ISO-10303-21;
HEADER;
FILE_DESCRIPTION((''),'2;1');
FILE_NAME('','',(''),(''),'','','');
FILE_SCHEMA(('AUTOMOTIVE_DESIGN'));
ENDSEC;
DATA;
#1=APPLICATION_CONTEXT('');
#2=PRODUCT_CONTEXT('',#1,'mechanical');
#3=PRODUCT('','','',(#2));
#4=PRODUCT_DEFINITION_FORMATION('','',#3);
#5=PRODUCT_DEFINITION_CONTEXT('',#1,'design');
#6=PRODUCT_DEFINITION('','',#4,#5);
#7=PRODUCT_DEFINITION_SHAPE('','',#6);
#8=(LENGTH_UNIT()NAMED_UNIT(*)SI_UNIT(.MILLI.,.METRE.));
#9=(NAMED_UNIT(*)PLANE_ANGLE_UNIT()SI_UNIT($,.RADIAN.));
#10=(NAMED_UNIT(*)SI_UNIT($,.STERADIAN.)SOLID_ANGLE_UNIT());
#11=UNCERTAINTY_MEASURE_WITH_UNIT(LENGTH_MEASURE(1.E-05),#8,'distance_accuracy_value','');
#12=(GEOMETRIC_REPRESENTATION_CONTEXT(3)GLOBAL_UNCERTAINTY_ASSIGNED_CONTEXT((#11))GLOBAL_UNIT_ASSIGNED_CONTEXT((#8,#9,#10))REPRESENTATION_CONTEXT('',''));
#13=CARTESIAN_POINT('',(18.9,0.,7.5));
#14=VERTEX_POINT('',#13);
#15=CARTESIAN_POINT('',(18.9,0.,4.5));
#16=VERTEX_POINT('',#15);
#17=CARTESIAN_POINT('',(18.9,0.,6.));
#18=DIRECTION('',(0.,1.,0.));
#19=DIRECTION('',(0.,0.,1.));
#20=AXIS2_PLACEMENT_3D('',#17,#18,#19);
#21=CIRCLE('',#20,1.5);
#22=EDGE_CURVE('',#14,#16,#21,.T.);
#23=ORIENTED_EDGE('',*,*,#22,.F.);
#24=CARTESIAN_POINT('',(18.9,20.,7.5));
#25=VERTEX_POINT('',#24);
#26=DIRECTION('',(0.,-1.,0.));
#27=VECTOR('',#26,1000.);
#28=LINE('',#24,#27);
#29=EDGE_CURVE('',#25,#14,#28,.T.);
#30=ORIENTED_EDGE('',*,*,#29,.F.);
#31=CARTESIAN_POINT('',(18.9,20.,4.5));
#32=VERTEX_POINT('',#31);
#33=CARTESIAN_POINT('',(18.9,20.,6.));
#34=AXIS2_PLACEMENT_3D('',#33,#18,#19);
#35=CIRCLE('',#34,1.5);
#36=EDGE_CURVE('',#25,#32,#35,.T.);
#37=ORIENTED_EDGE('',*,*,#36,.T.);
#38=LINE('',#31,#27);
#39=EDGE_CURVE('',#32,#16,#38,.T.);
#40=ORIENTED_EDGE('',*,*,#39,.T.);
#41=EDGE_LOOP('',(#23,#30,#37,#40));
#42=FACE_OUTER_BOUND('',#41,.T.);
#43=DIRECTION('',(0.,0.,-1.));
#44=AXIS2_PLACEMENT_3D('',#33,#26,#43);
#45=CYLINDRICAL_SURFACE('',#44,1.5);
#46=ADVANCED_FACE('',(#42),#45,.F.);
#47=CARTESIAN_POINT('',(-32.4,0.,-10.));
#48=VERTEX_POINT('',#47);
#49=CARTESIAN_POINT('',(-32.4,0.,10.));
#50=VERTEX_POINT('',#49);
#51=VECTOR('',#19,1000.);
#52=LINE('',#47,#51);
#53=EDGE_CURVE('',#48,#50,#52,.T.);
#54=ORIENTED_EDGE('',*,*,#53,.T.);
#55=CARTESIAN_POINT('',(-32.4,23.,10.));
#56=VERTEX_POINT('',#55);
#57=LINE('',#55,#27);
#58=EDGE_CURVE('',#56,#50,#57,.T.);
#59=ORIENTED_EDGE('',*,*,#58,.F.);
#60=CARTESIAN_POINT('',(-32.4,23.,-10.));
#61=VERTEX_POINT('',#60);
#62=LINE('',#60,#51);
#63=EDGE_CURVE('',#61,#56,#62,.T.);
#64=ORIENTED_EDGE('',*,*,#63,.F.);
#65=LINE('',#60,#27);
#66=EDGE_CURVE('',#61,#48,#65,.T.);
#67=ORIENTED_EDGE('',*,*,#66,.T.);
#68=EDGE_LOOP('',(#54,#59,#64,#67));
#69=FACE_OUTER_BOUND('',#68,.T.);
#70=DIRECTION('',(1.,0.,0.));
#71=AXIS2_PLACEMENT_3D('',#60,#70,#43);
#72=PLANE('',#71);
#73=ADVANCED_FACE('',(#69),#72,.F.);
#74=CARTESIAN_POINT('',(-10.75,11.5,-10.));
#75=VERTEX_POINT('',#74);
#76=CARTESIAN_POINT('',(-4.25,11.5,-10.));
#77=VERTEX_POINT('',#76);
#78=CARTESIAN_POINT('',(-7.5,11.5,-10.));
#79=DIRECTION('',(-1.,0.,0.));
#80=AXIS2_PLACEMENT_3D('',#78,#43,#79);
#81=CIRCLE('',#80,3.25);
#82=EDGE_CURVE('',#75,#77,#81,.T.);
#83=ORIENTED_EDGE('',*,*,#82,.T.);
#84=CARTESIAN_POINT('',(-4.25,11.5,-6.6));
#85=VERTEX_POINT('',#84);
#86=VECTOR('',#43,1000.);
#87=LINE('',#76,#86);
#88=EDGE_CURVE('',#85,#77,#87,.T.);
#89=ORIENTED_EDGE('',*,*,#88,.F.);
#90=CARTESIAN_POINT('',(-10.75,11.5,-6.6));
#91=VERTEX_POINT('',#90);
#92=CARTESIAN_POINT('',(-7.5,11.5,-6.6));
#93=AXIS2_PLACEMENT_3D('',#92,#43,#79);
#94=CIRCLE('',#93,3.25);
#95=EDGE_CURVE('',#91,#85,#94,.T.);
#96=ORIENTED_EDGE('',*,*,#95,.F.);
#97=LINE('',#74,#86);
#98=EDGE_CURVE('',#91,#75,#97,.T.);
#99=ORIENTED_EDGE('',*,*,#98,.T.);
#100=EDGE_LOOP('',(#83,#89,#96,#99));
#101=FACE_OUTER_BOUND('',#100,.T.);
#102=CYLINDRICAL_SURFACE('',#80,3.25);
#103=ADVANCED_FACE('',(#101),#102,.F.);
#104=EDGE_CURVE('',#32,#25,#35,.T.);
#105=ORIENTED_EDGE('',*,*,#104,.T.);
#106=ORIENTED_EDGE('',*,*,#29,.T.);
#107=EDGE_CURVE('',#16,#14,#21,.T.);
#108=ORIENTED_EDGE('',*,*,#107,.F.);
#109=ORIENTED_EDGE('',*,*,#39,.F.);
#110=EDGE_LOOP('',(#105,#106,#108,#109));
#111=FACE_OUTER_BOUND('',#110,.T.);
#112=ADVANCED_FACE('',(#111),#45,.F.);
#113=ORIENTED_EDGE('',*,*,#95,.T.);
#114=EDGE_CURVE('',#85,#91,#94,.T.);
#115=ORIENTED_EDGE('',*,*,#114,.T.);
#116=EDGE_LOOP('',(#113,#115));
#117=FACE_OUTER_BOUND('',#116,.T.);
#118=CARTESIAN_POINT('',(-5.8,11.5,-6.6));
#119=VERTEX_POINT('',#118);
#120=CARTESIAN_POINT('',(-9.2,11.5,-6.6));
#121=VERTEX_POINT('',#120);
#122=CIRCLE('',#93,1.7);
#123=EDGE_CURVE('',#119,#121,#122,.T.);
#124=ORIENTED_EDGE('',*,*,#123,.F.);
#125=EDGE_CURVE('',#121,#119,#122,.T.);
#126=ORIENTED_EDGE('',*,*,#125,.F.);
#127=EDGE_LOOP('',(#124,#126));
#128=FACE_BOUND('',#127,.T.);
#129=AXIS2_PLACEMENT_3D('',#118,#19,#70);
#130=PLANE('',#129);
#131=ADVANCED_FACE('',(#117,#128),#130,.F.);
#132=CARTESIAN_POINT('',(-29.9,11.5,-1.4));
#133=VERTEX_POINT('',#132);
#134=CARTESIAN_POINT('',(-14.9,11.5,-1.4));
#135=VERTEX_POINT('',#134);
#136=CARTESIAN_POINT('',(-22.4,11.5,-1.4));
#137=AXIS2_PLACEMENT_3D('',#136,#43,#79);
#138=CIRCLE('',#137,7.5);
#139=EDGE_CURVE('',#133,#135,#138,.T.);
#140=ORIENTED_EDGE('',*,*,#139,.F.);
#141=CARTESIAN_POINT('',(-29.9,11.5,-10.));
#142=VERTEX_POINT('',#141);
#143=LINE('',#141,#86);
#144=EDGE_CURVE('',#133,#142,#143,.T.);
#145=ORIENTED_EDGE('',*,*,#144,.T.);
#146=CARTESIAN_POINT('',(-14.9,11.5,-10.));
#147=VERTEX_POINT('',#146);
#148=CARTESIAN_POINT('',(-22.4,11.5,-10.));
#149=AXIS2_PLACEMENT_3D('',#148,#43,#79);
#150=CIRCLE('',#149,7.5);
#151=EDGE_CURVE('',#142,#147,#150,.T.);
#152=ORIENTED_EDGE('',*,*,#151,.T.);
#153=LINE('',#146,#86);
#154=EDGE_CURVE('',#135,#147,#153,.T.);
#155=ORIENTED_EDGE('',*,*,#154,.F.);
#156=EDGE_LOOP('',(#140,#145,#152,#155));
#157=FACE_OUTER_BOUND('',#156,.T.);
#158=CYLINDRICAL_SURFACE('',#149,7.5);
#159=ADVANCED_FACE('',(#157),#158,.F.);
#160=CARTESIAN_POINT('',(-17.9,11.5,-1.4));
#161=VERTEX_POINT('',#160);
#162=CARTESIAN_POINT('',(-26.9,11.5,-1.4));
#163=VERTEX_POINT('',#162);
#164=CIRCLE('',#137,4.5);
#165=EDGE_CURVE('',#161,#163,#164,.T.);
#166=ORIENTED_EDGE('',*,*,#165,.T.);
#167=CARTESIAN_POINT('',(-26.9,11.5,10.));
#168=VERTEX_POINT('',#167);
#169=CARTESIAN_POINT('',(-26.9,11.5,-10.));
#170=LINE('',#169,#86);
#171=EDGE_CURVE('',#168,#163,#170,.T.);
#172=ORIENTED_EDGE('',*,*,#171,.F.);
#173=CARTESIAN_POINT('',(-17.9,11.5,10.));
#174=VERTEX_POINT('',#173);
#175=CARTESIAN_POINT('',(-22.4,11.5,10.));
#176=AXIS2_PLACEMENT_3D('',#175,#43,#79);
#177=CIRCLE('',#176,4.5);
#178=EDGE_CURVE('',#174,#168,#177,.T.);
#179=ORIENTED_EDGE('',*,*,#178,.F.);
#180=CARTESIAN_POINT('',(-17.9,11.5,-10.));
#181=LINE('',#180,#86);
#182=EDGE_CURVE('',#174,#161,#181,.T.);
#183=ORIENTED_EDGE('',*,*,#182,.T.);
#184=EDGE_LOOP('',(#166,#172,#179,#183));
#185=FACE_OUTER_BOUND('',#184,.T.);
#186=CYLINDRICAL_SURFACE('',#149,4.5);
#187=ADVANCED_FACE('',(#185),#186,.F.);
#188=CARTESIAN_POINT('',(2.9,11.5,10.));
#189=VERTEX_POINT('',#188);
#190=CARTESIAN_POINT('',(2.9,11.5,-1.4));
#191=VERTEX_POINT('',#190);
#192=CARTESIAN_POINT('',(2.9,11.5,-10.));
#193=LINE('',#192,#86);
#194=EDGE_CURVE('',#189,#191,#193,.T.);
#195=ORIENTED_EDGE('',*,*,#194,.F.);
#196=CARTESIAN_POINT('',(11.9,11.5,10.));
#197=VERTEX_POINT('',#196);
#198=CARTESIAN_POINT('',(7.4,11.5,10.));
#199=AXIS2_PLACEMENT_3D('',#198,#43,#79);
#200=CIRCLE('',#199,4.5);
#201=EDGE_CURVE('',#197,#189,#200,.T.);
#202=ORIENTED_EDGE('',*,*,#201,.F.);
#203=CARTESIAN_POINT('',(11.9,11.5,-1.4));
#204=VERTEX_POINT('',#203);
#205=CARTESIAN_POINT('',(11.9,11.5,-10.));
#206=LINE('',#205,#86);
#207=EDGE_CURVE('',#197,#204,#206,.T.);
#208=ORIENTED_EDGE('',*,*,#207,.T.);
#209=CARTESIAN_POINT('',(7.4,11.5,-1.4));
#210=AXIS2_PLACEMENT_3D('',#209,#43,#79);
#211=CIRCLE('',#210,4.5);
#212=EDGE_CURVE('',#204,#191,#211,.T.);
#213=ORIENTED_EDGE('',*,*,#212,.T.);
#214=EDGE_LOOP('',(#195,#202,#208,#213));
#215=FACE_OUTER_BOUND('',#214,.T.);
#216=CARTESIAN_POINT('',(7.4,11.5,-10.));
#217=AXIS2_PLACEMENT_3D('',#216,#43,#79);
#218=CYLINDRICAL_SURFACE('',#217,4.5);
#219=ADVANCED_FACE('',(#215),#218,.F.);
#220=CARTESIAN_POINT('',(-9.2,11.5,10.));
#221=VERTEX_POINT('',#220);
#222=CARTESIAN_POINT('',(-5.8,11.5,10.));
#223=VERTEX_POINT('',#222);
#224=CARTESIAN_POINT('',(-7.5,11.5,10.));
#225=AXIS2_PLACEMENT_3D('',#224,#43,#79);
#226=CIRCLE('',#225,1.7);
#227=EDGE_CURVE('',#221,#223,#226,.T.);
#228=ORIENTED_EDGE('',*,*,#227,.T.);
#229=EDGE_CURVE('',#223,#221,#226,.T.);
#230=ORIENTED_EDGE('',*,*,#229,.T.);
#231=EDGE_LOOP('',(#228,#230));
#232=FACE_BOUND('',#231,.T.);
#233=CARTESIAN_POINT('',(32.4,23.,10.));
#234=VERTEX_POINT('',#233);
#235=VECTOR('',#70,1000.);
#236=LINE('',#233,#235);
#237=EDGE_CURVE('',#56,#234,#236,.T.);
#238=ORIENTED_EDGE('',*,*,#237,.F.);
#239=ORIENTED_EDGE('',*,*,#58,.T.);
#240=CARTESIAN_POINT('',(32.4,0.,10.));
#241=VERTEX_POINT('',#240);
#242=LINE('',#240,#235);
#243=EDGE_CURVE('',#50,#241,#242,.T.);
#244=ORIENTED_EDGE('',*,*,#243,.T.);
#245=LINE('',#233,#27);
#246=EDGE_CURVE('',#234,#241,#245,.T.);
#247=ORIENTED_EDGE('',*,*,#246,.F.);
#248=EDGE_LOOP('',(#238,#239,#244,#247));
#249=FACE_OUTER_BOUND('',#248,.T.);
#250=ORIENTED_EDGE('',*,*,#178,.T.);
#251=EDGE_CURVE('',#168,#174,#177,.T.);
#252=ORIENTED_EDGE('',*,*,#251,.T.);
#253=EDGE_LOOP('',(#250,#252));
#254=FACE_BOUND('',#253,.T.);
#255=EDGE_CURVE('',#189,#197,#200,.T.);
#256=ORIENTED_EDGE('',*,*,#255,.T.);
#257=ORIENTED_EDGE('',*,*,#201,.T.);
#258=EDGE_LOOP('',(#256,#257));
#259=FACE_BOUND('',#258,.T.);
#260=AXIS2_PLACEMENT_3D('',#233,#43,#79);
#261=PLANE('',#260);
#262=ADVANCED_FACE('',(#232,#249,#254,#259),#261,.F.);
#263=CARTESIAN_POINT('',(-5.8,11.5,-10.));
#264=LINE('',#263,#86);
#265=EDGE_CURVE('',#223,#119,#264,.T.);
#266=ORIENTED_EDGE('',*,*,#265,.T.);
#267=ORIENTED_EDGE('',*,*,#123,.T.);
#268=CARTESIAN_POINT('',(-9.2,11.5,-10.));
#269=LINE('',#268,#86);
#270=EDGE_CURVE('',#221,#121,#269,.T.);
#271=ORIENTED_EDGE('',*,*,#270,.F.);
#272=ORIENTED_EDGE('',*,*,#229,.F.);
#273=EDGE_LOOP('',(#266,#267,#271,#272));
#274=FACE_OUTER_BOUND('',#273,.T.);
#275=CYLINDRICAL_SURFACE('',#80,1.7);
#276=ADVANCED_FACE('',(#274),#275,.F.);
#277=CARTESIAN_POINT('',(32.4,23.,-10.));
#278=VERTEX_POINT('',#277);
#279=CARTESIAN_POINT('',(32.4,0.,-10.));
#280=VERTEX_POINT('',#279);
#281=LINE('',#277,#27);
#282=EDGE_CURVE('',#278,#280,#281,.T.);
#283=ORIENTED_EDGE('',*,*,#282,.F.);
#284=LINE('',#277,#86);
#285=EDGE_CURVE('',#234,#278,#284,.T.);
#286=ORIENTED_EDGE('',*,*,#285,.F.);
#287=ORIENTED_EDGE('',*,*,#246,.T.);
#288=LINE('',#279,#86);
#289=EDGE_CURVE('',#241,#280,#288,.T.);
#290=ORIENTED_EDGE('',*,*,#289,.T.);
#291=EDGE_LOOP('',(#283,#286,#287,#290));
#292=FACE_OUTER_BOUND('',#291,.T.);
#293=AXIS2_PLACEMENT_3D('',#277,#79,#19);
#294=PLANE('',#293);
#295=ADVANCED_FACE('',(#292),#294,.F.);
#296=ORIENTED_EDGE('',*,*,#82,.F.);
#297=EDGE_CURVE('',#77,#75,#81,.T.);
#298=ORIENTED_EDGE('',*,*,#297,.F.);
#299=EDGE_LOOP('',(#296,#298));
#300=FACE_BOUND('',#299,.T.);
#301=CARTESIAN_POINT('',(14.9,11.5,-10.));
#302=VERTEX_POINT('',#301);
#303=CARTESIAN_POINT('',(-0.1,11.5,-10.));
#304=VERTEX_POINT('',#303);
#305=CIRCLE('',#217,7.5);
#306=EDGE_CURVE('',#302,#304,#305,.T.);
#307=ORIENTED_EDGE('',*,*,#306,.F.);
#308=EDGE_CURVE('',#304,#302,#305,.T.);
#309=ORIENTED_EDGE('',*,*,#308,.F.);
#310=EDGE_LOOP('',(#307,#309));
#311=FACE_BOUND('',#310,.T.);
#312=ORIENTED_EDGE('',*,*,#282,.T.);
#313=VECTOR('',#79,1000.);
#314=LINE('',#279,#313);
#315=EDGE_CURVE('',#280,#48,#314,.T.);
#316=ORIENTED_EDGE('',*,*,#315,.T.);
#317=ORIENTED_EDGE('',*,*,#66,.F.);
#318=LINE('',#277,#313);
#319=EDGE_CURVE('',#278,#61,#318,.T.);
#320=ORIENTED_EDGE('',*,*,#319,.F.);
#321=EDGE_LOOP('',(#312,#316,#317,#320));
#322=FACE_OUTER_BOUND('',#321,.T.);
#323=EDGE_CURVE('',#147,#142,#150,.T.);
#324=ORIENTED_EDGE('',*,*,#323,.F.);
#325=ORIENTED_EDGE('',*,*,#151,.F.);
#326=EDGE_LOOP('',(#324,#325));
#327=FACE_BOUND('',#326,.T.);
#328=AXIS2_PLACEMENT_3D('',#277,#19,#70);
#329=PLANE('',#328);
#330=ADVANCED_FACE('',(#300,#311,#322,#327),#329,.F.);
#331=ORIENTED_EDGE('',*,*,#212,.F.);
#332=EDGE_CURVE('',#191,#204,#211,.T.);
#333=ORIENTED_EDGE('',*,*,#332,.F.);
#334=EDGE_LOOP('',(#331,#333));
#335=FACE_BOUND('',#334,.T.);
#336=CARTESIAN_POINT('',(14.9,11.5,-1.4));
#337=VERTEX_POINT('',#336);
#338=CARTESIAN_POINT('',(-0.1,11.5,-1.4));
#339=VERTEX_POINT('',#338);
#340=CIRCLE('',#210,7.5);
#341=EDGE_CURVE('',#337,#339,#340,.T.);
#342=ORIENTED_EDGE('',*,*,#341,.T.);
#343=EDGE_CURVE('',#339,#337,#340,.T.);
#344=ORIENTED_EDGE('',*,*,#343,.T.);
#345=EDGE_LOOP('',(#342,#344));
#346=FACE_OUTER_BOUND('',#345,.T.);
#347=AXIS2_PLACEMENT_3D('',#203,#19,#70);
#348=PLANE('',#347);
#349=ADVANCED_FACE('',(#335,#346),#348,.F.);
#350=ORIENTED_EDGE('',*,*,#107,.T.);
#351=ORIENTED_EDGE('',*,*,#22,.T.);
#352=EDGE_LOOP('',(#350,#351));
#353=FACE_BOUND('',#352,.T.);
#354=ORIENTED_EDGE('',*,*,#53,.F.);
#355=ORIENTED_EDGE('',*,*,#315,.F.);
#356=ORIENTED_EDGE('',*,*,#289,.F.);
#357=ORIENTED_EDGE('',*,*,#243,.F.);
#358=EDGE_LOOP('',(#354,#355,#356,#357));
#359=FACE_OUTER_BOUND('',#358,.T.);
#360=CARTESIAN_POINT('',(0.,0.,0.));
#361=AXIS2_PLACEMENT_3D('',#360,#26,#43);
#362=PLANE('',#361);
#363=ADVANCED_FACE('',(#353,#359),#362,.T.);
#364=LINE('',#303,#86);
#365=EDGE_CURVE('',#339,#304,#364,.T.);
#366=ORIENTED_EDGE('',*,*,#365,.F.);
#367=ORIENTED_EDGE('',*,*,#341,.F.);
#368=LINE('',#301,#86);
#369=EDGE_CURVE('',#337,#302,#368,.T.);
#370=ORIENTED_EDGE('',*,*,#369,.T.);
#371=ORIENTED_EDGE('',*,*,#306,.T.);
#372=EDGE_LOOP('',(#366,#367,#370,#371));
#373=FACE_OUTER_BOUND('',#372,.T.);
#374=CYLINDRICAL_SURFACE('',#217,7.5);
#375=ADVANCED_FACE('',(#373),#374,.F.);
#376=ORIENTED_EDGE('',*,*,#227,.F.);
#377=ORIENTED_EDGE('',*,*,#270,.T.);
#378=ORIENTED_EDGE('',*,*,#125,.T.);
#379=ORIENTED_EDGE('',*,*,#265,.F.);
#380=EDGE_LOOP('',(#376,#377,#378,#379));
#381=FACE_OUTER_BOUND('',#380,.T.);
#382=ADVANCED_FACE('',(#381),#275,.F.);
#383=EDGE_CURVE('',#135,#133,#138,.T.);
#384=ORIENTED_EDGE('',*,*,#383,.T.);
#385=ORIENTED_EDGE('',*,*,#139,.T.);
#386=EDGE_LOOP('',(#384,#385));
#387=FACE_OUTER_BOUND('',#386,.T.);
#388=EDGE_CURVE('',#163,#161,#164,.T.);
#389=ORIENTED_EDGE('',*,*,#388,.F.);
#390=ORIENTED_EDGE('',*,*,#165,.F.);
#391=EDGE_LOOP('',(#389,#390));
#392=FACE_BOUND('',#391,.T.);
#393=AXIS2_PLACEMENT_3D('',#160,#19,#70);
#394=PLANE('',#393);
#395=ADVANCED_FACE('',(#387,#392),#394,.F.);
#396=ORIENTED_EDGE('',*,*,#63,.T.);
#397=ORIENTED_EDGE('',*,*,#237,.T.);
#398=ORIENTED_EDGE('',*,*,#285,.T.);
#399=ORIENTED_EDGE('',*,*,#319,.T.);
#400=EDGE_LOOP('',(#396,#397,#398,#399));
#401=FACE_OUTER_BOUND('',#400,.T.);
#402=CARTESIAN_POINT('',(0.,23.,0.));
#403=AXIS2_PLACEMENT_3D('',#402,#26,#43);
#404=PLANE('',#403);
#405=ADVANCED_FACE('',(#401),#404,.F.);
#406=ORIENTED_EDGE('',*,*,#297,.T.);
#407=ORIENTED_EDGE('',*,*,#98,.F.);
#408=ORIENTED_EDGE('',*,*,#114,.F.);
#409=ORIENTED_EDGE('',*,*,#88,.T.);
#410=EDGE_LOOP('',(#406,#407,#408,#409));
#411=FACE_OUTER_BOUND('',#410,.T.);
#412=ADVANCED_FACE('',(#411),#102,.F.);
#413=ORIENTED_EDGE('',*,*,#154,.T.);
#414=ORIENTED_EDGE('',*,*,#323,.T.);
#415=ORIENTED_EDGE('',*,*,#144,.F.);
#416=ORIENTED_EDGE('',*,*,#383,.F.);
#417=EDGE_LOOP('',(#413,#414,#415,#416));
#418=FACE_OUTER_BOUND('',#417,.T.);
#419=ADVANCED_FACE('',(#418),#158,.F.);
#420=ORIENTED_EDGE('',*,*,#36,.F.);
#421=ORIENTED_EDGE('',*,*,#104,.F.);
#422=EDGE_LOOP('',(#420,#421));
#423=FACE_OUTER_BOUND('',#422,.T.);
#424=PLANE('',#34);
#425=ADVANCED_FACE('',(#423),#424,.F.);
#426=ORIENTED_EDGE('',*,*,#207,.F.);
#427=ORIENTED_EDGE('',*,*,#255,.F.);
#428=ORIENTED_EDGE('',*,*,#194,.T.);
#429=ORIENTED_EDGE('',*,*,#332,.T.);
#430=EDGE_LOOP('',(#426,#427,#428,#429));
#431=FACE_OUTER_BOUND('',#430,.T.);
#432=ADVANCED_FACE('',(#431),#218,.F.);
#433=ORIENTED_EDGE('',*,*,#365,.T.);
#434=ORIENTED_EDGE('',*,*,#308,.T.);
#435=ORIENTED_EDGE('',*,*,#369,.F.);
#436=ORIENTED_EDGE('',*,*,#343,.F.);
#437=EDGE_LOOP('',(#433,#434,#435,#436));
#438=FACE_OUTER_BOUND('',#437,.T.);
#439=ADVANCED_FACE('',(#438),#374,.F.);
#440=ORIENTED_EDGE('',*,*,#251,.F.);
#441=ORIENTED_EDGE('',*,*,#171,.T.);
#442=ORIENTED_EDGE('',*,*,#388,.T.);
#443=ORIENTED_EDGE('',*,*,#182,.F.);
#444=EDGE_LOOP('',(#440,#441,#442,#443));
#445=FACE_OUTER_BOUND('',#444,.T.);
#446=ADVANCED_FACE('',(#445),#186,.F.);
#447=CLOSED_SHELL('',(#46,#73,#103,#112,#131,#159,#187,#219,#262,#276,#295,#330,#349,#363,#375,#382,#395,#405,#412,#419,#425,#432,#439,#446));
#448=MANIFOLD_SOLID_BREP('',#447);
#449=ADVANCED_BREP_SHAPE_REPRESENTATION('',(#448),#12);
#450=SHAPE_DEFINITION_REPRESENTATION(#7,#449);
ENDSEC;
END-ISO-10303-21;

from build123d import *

# Parameters (mm, degrees)
SKETCH1_W                                           = 64.8
SKETCH1_H                                           = 20
BOSS_EXTRUDE1_DEPTH                                 = 23
SKETCH2_R                                           = 1.5
CUT_EXTRUDE1_DEPTH                                  = 20
CBORE_FOR_M8_HEX_SOCKET_HEAD_CAP_SCREW1_D           = 9
CBORE_FOR_M8_HEX_SOCKET_HEAD_CAP_SCREW1_DEPTH       = 41.94
CBORE_FOR_M8_HEX_SOCKET_HEAD_CAP_SCREW1_CBORE_D     = 15
CBORE_FOR_M8_HEX_SOCKET_HEAD_CAP_SCREW1_CBORE_DEPTH = 8.6
CBORE_FOR_M8_HEX_SOCKET_HEAD_CAP_SCREW1_TIP         = 2.703872786
CBORE_FOR_M3_HEX_SOCKET_HEAD_CAP_SCREW1_D           = 3.4
CBORE_FOR_M3_HEX_SOCKET_HEAD_CAP_SCREW1_DEPTH       = 41.94
CBORE_FOR_M3_HEX_SOCKET_HEAD_CAP_SCREW1_CBORE_D     = 6.5
CBORE_FOR_M3_HEX_SOCKET_HEAD_CAP_SCREW1_CBORE_DEPTH = 3.4
CBORE_FOR_M3_HEX_SOCKET_HEAD_CAP_SCREW1_TIP         = 1.021463052


with BuildPart() as part:
    # Sketch1 → Boss-Extrude1 (new body)
    with BuildSketch(Plane(origin=(0, 0, 0), x_dir=(1, 0, 0), z_dir=(0, 1, 0))):
        Rectangle(SKETCH1_W, SKETCH1_H)
    extrude(amount=BOSS_EXTRUDE1_DEPTH)

    # Sketch2 → Cut-Extrude1 (cut)
    with BuildSketch(Plane(origin=(0, 0, 0), x_dir=(1, 0, 0), z_dir=(0, 1, 0))):
        with Locations(Location((18.9, -6, 0), (0, 0, 270))):
            Circle(SKETCH2_R)
    extrude(amount=CUT_EXTRUDE1_DEPTH, mode=Mode.SUBTRACT)

    # CBORE for M8 Hex Socket Head Cap Screw1
    with Locations(Plane(origin=(-22.4, 11.5, -10), x_dir=(-1, 0, 0), z_dir=(0, 0, -1))):
        with Locations((0, 0), (-29.8, 0)):
            CounterBoreHole(CBORE_FOR_M8_HEX_SOCKET_HEAD_CAP_SCREW1_D / 2, CBORE_FOR_M8_HEX_SOCKET_HEAD_CAP_SCREW1_CBORE_D / 2, CBORE_FOR_M8_HEX_SOCKET_HEAD_CAP_SCREW1_CBORE_DEPTH, depth=CBORE_FOR_M8_HEX_SOCKET_HEAD_CAP_SCREW1_DEPTH)
            with Locations((0, 0, -(CBORE_FOR_M8_HEX_SOCKET_HEAD_CAP_SCREW1_DEPTH + CBORE_FOR_M8_HEX_SOCKET_HEAD_CAP_SCREW1_TIP / 2))):  # 118° drill point
                Cone(0, CBORE_FOR_M8_HEX_SOCKET_HEAD_CAP_SCREW1_D / 2, CBORE_FOR_M8_HEX_SOCKET_HEAD_CAP_SCREW1_TIP, mode=Mode.SUBTRACT)

    # CBORE for M3 Hex Socket Head Cap Screw1
    with Locations(Plane(origin=(-7.5, 11.5, -10), x_dir=(-1, 0, 0), z_dir=(0, 0, -1))):
        with Locations((0, 0)):
            CounterBoreHole(CBORE_FOR_M3_HEX_SOCKET_HEAD_CAP_SCREW1_D / 2, CBORE_FOR_M3_HEX_SOCKET_HEAD_CAP_SCREW1_CBORE_D / 2, CBORE_FOR_M3_HEX_SOCKET_HEAD_CAP_SCREW1_CBORE_DEPTH, depth=CBORE_FOR_M3_HEX_SOCKET_HEAD_CAP_SCREW1_DEPTH)
            with Locations((0, 0, -(CBORE_FOR_M3_HEX_SOCKET_HEAD_CAP_SCREW1_DEPTH + CBORE_FOR_M3_HEX_SOCKET_HEAD_CAP_SCREW1_TIP / 2))):  # 118° drill point
                Cone(0, CBORE_FOR_M3_HEX_SOCKET_HEAD_CAP_SCREW1_D / 2, CBORE_FOR_M3_HEX_SOCKET_HEAD_CAP_SCREW1_TIP, mode=Mode.SUBTRACT)


solid = part.part
